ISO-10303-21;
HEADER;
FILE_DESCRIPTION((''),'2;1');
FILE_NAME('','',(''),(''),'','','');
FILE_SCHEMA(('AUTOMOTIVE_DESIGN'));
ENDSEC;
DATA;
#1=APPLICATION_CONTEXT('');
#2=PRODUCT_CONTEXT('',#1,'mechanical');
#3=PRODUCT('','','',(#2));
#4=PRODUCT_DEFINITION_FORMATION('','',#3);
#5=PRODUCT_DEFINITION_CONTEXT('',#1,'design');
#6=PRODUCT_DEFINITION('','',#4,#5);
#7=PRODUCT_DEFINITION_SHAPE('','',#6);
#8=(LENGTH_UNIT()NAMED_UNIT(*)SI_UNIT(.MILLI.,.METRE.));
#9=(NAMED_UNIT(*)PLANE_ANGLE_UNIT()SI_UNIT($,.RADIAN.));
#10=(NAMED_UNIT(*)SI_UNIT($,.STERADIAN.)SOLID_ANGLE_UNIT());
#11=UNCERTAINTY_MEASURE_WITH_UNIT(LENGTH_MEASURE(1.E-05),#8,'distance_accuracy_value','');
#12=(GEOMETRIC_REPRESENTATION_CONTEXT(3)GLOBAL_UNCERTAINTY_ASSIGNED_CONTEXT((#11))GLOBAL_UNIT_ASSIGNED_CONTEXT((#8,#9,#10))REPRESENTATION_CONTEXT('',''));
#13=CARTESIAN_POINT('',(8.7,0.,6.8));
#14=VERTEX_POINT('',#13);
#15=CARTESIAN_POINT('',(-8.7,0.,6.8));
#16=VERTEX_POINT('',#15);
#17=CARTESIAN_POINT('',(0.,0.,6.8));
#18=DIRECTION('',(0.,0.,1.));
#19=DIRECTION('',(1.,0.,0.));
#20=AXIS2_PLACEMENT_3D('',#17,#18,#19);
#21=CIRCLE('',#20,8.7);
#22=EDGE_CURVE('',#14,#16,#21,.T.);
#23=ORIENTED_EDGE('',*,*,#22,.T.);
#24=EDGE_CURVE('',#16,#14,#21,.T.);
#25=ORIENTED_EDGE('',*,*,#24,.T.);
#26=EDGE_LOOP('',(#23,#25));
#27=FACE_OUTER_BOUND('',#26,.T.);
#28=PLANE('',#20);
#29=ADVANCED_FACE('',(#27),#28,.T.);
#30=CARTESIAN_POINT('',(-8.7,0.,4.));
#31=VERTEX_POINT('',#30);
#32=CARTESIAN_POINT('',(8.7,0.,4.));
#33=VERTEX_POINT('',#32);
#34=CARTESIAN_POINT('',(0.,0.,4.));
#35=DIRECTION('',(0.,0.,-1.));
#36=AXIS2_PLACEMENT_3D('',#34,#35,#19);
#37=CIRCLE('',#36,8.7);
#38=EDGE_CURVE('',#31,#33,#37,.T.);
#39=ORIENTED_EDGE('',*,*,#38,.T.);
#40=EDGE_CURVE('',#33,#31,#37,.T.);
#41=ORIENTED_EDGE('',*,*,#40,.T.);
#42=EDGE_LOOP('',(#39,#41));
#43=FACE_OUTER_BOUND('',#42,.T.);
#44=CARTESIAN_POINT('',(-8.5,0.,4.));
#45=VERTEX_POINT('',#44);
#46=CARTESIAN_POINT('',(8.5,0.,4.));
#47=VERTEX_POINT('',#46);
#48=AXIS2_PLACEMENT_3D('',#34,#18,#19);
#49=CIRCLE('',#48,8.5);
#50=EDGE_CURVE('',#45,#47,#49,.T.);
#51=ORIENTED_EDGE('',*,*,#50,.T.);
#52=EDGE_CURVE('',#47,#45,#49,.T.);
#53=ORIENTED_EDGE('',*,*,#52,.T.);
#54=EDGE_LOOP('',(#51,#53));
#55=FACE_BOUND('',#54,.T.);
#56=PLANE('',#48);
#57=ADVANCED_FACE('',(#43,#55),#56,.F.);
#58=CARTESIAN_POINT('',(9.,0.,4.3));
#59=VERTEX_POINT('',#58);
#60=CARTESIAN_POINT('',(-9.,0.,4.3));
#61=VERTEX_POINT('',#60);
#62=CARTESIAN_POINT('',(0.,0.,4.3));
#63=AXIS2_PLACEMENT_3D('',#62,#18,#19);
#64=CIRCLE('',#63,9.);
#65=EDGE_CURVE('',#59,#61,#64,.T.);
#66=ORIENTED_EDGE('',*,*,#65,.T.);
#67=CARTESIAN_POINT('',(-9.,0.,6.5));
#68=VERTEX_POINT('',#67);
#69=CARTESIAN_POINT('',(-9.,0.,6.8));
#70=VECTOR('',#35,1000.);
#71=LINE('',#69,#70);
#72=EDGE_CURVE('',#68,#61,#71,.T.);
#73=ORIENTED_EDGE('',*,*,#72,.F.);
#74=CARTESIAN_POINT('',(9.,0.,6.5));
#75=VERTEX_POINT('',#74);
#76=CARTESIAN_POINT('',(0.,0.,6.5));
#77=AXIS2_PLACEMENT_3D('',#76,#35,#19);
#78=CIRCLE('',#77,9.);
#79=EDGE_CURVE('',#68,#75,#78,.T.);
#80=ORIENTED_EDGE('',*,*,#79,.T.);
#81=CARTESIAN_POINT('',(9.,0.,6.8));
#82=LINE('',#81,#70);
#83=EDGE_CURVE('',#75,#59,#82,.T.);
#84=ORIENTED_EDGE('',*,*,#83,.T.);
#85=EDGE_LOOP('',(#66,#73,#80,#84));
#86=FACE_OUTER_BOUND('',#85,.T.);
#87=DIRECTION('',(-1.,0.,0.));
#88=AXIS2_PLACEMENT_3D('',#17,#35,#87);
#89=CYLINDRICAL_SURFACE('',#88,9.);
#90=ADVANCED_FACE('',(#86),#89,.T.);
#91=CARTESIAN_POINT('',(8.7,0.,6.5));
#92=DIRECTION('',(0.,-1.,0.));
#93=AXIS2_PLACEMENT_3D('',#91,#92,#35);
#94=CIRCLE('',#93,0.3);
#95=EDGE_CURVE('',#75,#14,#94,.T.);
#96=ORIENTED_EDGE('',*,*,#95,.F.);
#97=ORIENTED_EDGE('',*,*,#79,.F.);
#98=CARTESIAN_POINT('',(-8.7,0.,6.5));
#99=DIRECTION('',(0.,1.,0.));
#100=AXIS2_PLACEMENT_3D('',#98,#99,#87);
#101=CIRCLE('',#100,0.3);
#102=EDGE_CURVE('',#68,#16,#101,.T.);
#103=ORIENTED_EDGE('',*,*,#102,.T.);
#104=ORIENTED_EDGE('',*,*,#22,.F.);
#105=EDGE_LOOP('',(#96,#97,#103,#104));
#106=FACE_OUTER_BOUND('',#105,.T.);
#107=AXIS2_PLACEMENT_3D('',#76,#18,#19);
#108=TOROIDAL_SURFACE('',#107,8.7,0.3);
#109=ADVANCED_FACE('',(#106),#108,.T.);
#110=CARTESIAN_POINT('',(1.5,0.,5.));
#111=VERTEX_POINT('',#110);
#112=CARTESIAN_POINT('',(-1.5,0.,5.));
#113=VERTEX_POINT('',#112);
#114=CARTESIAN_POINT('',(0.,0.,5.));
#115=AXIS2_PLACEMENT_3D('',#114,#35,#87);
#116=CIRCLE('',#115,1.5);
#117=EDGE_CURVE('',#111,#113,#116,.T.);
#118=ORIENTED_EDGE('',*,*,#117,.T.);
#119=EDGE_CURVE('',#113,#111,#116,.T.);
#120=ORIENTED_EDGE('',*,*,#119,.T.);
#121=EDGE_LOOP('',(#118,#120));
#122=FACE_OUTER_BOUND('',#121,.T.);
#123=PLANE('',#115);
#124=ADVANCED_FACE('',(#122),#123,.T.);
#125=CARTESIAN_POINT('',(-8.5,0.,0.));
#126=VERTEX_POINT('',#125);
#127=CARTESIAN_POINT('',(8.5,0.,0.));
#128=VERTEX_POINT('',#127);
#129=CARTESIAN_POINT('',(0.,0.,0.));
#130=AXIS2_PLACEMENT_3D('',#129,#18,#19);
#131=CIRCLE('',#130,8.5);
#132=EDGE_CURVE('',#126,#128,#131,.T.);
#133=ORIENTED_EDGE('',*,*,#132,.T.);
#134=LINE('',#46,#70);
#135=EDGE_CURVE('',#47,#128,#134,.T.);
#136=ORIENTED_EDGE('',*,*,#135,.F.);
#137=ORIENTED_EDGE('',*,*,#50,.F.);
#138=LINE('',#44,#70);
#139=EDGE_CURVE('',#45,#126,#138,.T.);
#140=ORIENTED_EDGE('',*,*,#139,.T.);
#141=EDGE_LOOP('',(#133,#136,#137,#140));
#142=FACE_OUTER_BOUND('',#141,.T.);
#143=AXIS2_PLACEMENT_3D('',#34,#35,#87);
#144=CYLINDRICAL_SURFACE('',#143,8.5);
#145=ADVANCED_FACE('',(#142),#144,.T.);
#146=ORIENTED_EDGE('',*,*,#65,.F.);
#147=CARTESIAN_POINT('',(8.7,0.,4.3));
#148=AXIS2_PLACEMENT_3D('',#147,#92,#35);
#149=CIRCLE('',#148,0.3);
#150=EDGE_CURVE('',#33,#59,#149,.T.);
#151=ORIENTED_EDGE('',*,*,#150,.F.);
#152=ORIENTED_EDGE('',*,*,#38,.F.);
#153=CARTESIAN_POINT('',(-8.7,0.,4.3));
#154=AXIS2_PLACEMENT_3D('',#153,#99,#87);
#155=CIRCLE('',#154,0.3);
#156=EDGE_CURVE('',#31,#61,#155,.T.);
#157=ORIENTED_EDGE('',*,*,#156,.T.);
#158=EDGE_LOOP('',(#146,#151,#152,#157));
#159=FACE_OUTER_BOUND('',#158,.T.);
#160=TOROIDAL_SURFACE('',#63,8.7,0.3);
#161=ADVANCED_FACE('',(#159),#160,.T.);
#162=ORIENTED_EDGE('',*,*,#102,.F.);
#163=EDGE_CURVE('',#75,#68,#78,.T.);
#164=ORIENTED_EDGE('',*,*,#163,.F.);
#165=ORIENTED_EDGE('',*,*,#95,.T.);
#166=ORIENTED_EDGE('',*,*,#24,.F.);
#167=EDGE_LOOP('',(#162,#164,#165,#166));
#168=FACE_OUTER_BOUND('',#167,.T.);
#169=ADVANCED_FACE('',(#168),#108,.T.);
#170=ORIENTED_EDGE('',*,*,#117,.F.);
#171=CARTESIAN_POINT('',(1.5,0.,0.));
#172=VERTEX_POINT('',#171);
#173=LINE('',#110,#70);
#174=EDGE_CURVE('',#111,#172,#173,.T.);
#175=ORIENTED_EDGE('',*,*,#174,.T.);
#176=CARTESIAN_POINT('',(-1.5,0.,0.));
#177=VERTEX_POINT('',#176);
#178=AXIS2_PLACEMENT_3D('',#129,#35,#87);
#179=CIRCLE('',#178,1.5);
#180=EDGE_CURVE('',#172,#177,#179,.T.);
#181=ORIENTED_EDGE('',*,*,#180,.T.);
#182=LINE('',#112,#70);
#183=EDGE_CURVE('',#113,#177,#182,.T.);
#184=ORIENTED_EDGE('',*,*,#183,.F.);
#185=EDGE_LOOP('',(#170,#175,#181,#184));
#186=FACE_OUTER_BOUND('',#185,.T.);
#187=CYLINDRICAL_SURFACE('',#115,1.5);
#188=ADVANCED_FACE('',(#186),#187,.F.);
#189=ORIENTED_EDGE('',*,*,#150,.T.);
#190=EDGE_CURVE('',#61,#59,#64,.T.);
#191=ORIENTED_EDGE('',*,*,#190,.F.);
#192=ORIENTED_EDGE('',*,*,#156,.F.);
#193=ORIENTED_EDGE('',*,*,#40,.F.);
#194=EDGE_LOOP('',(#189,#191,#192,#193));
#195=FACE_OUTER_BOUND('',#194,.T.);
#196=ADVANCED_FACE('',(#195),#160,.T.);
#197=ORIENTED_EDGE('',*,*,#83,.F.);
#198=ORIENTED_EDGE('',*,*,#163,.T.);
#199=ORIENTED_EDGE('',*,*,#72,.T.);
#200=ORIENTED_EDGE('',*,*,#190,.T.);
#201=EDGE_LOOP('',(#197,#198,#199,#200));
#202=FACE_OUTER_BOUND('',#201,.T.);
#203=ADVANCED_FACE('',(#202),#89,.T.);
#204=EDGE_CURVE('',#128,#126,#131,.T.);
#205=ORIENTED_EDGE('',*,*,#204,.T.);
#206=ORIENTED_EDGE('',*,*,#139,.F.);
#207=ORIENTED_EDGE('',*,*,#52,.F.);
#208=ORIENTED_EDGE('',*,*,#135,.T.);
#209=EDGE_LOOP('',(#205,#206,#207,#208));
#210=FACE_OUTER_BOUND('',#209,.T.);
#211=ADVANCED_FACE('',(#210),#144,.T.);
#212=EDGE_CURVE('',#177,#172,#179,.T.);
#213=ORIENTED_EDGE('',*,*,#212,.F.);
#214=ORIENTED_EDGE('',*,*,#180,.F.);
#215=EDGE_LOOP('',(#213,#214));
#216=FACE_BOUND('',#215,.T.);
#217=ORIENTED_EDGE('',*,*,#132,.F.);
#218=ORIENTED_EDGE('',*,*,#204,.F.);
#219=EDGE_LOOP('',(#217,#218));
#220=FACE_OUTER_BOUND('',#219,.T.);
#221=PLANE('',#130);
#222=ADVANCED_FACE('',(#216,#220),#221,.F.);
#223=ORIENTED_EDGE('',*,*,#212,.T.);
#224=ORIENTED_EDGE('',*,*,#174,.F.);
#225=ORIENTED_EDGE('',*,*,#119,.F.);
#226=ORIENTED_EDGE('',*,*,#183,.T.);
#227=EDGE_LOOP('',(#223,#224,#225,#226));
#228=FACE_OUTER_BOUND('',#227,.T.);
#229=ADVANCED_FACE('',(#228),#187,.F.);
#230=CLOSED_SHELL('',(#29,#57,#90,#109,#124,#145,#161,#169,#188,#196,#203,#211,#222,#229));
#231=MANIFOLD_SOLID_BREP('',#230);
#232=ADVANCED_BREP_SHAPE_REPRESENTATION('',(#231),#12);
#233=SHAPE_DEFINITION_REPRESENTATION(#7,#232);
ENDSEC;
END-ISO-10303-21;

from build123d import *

# Parameters (mm, degrees)
SKETCH1_R           = 8.5
BOSS_EXTRUDE1_DEPTH = 4
SKETCH2_R           = 9
BOSS_EXTRUDE2_DEPTH = 2.8
FILLET1_R           = 0.3
SKETCH3_R           = 1.5
CUT_EXTRUDE1_DEPTH  = 5


with BuildPart() as part:
    # Sketch1 → Boss-Extrude1 (new body)
    with BuildSketch(Plane.XY):
        Circle(SKETCH1_R)
    extrude(amount=BOSS_EXTRUDE1_DEPTH)

    # Sketch2 → Boss-Extrude2 (add)
    with BuildSketch(Plane.XY.offset(4)):
        Circle(SKETCH2_R)
    extrude(amount=BOSS_EXTRUDE2_DEPTH)

    # Fillet1
    fillet1_edges = [part.edges().sort_by_distance(p)[0] for p in [
        (-9, 0, 4),
        (-9, 0, 6.8),
    ]]
    fillet(fillet1_edges, radius=FILLET1_R)

    # Sketch3 → Cut-Extrude1 (cut)
    with BuildSketch(Plane(origin=(0, 0, 0), x_dir=(-1, 0, 0), z_dir=(0, 0, -1))):
        Circle(SKETCH3_R)
    extrude(amount=-CUT_EXTRUDE1_DEPTH, mode=Mode.SUBTRACT)


solid = part.part
